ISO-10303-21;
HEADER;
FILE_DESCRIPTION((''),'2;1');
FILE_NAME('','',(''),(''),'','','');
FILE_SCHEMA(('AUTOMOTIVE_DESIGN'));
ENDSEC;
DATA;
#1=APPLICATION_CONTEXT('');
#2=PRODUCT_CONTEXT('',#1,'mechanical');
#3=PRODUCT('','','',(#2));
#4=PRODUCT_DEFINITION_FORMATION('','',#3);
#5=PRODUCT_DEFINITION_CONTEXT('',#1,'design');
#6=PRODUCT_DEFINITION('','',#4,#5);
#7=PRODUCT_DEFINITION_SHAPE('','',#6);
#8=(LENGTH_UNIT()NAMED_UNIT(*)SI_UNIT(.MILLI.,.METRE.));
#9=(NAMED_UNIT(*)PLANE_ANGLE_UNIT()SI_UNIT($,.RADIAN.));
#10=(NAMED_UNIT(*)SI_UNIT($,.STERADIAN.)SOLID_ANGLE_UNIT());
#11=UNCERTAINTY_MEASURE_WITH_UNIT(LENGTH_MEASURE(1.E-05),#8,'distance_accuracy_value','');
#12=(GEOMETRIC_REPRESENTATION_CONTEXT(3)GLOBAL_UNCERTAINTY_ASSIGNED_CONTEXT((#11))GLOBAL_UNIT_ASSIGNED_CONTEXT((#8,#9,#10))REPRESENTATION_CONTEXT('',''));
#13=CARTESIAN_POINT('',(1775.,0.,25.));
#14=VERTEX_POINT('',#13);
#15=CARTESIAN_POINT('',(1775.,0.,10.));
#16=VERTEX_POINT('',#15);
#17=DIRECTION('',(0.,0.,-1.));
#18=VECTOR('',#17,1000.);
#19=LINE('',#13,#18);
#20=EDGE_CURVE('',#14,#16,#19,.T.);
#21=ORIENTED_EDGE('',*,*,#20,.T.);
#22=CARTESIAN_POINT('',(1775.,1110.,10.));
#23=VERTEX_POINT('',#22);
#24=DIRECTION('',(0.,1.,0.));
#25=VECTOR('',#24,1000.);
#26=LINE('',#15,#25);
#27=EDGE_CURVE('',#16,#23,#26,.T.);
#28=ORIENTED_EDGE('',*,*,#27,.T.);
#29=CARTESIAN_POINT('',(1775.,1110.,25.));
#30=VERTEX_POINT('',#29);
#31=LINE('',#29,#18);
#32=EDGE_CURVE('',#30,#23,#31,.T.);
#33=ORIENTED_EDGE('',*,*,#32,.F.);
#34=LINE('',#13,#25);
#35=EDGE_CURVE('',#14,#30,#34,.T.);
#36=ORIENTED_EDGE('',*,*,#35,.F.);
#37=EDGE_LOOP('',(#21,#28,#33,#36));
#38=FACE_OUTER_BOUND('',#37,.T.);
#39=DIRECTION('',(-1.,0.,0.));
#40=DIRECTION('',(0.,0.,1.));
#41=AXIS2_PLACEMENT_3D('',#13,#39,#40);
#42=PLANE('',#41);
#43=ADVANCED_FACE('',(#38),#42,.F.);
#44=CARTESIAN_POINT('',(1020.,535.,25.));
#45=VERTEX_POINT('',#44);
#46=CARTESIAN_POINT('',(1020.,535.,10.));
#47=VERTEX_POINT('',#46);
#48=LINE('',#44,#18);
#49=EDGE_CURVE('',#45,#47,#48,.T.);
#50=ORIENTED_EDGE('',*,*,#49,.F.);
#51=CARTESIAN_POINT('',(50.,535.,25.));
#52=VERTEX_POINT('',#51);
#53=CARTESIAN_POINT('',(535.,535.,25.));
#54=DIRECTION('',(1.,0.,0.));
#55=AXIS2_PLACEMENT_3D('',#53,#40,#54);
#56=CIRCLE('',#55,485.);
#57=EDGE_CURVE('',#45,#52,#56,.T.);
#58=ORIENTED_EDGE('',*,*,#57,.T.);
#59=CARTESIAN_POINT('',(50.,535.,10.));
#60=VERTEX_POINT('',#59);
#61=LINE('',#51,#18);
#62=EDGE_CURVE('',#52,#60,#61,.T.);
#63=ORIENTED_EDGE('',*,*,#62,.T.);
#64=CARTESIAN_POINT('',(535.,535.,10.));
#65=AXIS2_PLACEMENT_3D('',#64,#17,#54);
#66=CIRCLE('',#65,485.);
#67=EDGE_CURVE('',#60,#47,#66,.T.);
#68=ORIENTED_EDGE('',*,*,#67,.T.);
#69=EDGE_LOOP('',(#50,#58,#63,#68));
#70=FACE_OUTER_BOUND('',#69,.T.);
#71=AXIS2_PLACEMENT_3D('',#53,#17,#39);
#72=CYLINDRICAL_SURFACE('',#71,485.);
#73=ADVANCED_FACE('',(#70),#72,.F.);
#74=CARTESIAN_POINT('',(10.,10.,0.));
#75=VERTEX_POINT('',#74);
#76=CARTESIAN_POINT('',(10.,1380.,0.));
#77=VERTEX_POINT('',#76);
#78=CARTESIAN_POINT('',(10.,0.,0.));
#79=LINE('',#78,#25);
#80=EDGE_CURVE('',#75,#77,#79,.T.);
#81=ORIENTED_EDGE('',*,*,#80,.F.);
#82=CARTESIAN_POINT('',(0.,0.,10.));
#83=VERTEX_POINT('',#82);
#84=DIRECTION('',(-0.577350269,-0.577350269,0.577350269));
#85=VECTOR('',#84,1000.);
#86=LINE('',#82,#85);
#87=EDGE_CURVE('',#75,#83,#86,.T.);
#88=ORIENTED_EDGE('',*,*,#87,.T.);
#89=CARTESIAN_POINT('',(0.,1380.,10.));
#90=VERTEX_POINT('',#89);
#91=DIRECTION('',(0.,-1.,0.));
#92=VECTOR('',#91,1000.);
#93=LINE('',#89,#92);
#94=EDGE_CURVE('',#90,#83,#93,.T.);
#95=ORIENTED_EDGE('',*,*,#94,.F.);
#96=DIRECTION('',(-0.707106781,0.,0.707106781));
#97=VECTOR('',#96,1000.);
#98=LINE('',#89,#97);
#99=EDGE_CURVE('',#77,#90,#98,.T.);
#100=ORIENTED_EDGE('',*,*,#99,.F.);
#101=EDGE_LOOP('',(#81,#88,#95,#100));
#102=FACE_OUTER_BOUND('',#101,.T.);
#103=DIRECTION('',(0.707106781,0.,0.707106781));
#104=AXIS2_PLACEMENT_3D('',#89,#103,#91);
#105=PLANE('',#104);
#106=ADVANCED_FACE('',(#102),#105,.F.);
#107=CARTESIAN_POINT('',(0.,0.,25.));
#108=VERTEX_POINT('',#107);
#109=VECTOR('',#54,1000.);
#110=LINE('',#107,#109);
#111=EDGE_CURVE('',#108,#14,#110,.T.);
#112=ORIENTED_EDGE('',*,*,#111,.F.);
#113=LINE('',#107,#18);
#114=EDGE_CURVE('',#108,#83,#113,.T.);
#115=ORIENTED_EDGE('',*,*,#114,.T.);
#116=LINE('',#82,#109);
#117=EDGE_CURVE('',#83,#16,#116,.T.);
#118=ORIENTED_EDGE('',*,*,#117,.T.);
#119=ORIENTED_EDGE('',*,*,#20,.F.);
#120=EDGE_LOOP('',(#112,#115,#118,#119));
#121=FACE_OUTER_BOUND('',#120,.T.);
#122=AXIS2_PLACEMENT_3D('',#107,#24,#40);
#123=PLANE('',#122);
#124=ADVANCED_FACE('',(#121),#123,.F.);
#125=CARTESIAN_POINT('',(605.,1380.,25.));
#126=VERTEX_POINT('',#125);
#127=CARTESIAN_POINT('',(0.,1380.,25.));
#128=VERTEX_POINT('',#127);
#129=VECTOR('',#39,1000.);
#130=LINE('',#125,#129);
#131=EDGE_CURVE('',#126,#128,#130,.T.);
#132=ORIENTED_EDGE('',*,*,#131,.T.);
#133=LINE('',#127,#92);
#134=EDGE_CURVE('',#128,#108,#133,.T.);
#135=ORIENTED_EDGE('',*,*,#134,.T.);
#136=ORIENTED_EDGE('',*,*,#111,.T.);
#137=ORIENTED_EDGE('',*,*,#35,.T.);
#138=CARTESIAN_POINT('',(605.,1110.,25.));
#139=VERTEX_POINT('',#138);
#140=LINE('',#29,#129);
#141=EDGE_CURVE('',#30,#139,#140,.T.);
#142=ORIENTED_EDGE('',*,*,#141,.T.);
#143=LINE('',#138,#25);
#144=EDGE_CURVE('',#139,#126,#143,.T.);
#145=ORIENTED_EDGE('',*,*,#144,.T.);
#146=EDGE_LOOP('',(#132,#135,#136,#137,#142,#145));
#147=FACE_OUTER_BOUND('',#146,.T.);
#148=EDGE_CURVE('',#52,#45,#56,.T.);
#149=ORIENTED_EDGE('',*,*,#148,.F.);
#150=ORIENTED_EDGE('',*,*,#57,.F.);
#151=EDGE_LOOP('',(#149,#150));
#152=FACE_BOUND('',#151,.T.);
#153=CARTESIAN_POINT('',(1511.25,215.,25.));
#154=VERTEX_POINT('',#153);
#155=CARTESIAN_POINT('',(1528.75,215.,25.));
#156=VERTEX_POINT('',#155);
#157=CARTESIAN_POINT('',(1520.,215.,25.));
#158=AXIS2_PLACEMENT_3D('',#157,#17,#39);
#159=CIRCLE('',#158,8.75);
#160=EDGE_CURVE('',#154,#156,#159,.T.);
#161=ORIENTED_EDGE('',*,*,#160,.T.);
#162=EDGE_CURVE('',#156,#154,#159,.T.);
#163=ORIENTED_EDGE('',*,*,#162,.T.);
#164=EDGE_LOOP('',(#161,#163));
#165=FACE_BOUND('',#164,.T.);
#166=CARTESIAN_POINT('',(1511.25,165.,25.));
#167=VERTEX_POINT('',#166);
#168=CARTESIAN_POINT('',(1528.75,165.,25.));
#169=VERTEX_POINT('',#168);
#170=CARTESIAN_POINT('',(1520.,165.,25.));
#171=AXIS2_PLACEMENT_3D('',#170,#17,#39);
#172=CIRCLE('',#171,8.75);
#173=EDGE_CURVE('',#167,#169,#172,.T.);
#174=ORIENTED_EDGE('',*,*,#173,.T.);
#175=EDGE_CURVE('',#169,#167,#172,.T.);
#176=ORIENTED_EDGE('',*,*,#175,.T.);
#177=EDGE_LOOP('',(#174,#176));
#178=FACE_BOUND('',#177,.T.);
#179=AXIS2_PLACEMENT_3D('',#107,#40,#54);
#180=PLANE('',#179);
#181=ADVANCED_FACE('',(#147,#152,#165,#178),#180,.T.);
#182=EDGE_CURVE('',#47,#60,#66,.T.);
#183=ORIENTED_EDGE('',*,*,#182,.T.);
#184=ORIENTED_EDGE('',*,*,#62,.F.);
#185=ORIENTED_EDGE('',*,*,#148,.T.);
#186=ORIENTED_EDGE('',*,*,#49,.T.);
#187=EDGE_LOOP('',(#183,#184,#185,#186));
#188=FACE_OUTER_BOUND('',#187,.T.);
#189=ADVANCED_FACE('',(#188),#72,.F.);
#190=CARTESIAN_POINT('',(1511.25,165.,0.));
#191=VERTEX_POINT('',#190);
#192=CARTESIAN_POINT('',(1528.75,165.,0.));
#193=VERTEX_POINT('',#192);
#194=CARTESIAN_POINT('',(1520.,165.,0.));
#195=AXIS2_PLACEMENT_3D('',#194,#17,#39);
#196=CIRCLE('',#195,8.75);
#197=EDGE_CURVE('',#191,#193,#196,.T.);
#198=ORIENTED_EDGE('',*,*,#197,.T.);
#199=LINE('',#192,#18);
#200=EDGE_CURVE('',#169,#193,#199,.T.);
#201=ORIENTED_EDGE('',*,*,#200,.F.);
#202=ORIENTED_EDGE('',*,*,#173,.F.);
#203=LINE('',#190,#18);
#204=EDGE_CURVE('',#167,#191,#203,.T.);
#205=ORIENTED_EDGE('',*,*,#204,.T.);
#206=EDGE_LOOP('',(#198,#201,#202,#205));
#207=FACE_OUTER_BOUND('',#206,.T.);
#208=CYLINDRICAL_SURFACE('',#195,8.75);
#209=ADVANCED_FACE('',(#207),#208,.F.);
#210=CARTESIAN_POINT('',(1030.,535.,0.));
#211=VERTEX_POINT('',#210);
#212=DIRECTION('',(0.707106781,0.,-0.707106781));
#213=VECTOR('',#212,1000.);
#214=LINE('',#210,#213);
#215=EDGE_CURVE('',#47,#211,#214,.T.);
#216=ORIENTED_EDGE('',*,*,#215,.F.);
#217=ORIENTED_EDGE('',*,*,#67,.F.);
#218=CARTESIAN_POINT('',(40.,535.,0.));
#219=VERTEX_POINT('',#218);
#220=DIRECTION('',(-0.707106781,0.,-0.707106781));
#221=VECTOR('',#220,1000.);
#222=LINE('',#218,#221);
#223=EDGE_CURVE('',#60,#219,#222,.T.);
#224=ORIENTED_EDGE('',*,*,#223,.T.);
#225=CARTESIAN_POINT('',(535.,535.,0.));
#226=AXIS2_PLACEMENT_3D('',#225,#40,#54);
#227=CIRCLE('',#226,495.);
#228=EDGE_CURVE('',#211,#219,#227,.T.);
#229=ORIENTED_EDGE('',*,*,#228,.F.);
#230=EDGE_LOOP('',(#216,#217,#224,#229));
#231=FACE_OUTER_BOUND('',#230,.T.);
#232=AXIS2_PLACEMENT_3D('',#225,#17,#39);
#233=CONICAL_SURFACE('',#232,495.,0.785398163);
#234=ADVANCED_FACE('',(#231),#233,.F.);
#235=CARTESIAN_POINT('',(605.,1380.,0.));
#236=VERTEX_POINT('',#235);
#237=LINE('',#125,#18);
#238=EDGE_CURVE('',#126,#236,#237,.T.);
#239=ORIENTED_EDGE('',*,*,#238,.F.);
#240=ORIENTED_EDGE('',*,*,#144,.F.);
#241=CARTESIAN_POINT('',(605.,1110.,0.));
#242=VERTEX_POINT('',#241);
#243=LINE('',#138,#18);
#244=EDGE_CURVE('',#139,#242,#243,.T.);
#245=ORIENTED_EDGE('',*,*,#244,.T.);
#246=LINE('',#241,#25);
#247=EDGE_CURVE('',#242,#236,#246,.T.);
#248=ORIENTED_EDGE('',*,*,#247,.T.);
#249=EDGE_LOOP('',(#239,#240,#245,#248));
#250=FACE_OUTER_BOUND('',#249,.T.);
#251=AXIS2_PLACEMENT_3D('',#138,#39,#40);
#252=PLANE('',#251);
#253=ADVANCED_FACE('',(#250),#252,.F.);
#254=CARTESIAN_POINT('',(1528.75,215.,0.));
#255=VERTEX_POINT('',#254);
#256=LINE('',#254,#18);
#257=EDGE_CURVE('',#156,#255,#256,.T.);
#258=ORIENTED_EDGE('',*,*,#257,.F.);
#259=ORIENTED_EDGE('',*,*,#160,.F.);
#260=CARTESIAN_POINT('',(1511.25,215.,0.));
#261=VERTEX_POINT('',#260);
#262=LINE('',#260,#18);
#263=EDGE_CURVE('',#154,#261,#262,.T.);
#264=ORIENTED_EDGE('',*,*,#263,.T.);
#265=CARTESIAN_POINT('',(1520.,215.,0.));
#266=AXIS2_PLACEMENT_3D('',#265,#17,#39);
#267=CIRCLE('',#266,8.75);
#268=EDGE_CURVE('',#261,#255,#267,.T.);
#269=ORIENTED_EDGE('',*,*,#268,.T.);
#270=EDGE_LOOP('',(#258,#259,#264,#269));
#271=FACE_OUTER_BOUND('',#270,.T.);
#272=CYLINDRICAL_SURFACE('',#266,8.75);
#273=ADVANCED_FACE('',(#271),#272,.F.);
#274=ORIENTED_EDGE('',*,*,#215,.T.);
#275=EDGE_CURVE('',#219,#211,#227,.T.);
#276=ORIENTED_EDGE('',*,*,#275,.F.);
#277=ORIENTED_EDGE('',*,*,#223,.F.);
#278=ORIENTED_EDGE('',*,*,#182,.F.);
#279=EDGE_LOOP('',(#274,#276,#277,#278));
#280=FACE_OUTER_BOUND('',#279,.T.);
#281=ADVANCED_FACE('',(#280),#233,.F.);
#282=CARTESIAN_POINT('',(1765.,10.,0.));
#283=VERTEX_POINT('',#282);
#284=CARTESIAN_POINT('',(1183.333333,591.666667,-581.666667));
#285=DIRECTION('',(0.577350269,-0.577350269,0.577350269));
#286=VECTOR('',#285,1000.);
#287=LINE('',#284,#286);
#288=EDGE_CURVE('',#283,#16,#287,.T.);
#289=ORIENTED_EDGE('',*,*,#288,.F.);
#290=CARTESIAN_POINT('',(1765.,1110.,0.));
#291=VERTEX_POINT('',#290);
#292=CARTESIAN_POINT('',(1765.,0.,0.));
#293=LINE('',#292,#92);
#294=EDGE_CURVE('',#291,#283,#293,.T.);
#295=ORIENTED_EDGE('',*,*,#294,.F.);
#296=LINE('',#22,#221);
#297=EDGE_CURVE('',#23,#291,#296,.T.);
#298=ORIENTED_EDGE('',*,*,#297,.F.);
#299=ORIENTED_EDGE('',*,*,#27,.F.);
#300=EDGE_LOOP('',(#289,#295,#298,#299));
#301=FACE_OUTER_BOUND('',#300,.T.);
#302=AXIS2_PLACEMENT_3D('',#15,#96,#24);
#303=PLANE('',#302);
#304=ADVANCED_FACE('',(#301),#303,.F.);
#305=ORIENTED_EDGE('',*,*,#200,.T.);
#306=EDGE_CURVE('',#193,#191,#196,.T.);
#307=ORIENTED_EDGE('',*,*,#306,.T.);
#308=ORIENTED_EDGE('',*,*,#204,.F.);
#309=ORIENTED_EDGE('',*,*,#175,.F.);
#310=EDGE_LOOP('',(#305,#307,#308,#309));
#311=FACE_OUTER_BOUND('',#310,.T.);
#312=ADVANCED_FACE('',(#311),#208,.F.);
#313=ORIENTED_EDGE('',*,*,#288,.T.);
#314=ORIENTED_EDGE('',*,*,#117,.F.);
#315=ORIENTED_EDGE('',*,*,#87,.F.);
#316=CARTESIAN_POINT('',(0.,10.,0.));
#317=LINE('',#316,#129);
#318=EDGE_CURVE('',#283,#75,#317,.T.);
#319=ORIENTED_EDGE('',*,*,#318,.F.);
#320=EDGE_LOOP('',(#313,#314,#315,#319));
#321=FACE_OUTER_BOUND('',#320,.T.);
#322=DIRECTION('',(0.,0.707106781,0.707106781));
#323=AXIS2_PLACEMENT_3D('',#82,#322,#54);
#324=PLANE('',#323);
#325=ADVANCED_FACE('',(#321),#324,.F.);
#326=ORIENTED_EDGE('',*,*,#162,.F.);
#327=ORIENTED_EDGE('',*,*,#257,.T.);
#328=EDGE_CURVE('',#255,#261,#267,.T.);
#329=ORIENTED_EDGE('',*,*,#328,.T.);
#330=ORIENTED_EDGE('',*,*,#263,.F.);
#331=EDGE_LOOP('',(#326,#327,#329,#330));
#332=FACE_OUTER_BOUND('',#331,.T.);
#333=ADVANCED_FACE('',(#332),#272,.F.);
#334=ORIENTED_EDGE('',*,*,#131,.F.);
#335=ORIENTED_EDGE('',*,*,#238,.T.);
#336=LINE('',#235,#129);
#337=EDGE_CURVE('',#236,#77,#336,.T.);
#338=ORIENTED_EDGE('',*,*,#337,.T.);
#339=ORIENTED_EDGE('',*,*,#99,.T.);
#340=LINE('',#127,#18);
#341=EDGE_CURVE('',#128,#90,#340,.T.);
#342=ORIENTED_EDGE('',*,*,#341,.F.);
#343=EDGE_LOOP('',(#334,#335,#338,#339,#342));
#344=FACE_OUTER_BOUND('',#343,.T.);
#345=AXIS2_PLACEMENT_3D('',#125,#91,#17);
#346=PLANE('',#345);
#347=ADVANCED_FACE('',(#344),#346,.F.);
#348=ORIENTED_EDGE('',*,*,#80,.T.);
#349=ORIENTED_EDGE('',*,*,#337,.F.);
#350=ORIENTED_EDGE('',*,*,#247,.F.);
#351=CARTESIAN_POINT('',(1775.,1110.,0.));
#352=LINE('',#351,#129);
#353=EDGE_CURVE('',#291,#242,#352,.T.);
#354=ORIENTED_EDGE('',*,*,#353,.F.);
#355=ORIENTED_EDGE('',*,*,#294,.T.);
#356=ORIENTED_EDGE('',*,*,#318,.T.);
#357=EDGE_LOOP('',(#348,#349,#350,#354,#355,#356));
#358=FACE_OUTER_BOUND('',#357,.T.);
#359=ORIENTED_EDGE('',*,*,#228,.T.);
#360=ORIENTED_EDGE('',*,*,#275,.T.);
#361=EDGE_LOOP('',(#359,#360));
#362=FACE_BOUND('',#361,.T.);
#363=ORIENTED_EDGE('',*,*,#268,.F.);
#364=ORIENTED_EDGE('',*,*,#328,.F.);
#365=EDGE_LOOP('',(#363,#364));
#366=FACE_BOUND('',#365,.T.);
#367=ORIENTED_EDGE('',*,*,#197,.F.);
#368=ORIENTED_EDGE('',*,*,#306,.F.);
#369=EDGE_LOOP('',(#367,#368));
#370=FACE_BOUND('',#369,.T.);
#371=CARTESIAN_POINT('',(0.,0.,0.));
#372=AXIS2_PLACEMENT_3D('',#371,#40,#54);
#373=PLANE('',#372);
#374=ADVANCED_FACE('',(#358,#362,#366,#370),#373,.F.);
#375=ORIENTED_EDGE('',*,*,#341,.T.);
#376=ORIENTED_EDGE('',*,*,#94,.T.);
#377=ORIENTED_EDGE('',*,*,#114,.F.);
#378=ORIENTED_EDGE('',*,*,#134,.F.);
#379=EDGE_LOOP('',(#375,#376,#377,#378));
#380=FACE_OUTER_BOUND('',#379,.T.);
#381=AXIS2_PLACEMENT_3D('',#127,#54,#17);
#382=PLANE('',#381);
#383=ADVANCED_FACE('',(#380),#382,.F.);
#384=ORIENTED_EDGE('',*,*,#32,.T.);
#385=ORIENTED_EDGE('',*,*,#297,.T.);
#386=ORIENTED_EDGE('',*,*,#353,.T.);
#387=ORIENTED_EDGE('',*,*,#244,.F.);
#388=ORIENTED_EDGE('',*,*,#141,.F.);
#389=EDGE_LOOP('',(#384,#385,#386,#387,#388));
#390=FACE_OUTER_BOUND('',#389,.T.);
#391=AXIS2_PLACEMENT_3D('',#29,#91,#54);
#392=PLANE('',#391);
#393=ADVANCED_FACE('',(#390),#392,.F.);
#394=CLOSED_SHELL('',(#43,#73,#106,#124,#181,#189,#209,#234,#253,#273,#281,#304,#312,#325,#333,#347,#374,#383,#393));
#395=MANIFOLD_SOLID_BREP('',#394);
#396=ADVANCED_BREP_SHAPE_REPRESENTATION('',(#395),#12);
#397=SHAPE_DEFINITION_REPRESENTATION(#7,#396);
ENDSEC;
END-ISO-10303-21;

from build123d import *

# Parameters (mm, degrees)
SKETCH1_R            = 485
BOSS_EXTRUDE1_DEPTH  = 25
CHAMFER1_SIZE        = 10
M20_THREADED_HOLE1_D = 17.5


with BuildPart() as part:
    # Sketch1 → Boss-Extrude1 (new body)
    with BuildSketch(Plane.XY):
        Polygon((0, 0), (1775, 0), (1775, 1110), (605, 1110), (605, 1380), (0, 1380), align=None)
        with Locations((535, 535)):
            Circle(SKETCH1_R, mode=Mode.SUBTRACT)
    extrude(amount=BOSS_EXTRUDE1_DEPTH)

    # Chamfer1
    chamfer1_edges = [part.edges().sort_by_distance(p)[0] for p in [
        (50, 535, 0),
        (1775, 555, 0),
        (887.5, 0, 0),
        (0, 690, 0),
    ]]
    chamfer(chamfer1_edges, length=CHAMFER1_SIZE)

    # M20 Threaded hole1 (through all)
    with Locations(Plane(origin=(1520, 215, 0), x_dir=(-1, 0, 0), z_dir=(0, 0, -1))):
        with Locations((0, 0), (0, -50)):
            Hole(M20_THREADED_HOLE1_D / 2)


solid = part.part
